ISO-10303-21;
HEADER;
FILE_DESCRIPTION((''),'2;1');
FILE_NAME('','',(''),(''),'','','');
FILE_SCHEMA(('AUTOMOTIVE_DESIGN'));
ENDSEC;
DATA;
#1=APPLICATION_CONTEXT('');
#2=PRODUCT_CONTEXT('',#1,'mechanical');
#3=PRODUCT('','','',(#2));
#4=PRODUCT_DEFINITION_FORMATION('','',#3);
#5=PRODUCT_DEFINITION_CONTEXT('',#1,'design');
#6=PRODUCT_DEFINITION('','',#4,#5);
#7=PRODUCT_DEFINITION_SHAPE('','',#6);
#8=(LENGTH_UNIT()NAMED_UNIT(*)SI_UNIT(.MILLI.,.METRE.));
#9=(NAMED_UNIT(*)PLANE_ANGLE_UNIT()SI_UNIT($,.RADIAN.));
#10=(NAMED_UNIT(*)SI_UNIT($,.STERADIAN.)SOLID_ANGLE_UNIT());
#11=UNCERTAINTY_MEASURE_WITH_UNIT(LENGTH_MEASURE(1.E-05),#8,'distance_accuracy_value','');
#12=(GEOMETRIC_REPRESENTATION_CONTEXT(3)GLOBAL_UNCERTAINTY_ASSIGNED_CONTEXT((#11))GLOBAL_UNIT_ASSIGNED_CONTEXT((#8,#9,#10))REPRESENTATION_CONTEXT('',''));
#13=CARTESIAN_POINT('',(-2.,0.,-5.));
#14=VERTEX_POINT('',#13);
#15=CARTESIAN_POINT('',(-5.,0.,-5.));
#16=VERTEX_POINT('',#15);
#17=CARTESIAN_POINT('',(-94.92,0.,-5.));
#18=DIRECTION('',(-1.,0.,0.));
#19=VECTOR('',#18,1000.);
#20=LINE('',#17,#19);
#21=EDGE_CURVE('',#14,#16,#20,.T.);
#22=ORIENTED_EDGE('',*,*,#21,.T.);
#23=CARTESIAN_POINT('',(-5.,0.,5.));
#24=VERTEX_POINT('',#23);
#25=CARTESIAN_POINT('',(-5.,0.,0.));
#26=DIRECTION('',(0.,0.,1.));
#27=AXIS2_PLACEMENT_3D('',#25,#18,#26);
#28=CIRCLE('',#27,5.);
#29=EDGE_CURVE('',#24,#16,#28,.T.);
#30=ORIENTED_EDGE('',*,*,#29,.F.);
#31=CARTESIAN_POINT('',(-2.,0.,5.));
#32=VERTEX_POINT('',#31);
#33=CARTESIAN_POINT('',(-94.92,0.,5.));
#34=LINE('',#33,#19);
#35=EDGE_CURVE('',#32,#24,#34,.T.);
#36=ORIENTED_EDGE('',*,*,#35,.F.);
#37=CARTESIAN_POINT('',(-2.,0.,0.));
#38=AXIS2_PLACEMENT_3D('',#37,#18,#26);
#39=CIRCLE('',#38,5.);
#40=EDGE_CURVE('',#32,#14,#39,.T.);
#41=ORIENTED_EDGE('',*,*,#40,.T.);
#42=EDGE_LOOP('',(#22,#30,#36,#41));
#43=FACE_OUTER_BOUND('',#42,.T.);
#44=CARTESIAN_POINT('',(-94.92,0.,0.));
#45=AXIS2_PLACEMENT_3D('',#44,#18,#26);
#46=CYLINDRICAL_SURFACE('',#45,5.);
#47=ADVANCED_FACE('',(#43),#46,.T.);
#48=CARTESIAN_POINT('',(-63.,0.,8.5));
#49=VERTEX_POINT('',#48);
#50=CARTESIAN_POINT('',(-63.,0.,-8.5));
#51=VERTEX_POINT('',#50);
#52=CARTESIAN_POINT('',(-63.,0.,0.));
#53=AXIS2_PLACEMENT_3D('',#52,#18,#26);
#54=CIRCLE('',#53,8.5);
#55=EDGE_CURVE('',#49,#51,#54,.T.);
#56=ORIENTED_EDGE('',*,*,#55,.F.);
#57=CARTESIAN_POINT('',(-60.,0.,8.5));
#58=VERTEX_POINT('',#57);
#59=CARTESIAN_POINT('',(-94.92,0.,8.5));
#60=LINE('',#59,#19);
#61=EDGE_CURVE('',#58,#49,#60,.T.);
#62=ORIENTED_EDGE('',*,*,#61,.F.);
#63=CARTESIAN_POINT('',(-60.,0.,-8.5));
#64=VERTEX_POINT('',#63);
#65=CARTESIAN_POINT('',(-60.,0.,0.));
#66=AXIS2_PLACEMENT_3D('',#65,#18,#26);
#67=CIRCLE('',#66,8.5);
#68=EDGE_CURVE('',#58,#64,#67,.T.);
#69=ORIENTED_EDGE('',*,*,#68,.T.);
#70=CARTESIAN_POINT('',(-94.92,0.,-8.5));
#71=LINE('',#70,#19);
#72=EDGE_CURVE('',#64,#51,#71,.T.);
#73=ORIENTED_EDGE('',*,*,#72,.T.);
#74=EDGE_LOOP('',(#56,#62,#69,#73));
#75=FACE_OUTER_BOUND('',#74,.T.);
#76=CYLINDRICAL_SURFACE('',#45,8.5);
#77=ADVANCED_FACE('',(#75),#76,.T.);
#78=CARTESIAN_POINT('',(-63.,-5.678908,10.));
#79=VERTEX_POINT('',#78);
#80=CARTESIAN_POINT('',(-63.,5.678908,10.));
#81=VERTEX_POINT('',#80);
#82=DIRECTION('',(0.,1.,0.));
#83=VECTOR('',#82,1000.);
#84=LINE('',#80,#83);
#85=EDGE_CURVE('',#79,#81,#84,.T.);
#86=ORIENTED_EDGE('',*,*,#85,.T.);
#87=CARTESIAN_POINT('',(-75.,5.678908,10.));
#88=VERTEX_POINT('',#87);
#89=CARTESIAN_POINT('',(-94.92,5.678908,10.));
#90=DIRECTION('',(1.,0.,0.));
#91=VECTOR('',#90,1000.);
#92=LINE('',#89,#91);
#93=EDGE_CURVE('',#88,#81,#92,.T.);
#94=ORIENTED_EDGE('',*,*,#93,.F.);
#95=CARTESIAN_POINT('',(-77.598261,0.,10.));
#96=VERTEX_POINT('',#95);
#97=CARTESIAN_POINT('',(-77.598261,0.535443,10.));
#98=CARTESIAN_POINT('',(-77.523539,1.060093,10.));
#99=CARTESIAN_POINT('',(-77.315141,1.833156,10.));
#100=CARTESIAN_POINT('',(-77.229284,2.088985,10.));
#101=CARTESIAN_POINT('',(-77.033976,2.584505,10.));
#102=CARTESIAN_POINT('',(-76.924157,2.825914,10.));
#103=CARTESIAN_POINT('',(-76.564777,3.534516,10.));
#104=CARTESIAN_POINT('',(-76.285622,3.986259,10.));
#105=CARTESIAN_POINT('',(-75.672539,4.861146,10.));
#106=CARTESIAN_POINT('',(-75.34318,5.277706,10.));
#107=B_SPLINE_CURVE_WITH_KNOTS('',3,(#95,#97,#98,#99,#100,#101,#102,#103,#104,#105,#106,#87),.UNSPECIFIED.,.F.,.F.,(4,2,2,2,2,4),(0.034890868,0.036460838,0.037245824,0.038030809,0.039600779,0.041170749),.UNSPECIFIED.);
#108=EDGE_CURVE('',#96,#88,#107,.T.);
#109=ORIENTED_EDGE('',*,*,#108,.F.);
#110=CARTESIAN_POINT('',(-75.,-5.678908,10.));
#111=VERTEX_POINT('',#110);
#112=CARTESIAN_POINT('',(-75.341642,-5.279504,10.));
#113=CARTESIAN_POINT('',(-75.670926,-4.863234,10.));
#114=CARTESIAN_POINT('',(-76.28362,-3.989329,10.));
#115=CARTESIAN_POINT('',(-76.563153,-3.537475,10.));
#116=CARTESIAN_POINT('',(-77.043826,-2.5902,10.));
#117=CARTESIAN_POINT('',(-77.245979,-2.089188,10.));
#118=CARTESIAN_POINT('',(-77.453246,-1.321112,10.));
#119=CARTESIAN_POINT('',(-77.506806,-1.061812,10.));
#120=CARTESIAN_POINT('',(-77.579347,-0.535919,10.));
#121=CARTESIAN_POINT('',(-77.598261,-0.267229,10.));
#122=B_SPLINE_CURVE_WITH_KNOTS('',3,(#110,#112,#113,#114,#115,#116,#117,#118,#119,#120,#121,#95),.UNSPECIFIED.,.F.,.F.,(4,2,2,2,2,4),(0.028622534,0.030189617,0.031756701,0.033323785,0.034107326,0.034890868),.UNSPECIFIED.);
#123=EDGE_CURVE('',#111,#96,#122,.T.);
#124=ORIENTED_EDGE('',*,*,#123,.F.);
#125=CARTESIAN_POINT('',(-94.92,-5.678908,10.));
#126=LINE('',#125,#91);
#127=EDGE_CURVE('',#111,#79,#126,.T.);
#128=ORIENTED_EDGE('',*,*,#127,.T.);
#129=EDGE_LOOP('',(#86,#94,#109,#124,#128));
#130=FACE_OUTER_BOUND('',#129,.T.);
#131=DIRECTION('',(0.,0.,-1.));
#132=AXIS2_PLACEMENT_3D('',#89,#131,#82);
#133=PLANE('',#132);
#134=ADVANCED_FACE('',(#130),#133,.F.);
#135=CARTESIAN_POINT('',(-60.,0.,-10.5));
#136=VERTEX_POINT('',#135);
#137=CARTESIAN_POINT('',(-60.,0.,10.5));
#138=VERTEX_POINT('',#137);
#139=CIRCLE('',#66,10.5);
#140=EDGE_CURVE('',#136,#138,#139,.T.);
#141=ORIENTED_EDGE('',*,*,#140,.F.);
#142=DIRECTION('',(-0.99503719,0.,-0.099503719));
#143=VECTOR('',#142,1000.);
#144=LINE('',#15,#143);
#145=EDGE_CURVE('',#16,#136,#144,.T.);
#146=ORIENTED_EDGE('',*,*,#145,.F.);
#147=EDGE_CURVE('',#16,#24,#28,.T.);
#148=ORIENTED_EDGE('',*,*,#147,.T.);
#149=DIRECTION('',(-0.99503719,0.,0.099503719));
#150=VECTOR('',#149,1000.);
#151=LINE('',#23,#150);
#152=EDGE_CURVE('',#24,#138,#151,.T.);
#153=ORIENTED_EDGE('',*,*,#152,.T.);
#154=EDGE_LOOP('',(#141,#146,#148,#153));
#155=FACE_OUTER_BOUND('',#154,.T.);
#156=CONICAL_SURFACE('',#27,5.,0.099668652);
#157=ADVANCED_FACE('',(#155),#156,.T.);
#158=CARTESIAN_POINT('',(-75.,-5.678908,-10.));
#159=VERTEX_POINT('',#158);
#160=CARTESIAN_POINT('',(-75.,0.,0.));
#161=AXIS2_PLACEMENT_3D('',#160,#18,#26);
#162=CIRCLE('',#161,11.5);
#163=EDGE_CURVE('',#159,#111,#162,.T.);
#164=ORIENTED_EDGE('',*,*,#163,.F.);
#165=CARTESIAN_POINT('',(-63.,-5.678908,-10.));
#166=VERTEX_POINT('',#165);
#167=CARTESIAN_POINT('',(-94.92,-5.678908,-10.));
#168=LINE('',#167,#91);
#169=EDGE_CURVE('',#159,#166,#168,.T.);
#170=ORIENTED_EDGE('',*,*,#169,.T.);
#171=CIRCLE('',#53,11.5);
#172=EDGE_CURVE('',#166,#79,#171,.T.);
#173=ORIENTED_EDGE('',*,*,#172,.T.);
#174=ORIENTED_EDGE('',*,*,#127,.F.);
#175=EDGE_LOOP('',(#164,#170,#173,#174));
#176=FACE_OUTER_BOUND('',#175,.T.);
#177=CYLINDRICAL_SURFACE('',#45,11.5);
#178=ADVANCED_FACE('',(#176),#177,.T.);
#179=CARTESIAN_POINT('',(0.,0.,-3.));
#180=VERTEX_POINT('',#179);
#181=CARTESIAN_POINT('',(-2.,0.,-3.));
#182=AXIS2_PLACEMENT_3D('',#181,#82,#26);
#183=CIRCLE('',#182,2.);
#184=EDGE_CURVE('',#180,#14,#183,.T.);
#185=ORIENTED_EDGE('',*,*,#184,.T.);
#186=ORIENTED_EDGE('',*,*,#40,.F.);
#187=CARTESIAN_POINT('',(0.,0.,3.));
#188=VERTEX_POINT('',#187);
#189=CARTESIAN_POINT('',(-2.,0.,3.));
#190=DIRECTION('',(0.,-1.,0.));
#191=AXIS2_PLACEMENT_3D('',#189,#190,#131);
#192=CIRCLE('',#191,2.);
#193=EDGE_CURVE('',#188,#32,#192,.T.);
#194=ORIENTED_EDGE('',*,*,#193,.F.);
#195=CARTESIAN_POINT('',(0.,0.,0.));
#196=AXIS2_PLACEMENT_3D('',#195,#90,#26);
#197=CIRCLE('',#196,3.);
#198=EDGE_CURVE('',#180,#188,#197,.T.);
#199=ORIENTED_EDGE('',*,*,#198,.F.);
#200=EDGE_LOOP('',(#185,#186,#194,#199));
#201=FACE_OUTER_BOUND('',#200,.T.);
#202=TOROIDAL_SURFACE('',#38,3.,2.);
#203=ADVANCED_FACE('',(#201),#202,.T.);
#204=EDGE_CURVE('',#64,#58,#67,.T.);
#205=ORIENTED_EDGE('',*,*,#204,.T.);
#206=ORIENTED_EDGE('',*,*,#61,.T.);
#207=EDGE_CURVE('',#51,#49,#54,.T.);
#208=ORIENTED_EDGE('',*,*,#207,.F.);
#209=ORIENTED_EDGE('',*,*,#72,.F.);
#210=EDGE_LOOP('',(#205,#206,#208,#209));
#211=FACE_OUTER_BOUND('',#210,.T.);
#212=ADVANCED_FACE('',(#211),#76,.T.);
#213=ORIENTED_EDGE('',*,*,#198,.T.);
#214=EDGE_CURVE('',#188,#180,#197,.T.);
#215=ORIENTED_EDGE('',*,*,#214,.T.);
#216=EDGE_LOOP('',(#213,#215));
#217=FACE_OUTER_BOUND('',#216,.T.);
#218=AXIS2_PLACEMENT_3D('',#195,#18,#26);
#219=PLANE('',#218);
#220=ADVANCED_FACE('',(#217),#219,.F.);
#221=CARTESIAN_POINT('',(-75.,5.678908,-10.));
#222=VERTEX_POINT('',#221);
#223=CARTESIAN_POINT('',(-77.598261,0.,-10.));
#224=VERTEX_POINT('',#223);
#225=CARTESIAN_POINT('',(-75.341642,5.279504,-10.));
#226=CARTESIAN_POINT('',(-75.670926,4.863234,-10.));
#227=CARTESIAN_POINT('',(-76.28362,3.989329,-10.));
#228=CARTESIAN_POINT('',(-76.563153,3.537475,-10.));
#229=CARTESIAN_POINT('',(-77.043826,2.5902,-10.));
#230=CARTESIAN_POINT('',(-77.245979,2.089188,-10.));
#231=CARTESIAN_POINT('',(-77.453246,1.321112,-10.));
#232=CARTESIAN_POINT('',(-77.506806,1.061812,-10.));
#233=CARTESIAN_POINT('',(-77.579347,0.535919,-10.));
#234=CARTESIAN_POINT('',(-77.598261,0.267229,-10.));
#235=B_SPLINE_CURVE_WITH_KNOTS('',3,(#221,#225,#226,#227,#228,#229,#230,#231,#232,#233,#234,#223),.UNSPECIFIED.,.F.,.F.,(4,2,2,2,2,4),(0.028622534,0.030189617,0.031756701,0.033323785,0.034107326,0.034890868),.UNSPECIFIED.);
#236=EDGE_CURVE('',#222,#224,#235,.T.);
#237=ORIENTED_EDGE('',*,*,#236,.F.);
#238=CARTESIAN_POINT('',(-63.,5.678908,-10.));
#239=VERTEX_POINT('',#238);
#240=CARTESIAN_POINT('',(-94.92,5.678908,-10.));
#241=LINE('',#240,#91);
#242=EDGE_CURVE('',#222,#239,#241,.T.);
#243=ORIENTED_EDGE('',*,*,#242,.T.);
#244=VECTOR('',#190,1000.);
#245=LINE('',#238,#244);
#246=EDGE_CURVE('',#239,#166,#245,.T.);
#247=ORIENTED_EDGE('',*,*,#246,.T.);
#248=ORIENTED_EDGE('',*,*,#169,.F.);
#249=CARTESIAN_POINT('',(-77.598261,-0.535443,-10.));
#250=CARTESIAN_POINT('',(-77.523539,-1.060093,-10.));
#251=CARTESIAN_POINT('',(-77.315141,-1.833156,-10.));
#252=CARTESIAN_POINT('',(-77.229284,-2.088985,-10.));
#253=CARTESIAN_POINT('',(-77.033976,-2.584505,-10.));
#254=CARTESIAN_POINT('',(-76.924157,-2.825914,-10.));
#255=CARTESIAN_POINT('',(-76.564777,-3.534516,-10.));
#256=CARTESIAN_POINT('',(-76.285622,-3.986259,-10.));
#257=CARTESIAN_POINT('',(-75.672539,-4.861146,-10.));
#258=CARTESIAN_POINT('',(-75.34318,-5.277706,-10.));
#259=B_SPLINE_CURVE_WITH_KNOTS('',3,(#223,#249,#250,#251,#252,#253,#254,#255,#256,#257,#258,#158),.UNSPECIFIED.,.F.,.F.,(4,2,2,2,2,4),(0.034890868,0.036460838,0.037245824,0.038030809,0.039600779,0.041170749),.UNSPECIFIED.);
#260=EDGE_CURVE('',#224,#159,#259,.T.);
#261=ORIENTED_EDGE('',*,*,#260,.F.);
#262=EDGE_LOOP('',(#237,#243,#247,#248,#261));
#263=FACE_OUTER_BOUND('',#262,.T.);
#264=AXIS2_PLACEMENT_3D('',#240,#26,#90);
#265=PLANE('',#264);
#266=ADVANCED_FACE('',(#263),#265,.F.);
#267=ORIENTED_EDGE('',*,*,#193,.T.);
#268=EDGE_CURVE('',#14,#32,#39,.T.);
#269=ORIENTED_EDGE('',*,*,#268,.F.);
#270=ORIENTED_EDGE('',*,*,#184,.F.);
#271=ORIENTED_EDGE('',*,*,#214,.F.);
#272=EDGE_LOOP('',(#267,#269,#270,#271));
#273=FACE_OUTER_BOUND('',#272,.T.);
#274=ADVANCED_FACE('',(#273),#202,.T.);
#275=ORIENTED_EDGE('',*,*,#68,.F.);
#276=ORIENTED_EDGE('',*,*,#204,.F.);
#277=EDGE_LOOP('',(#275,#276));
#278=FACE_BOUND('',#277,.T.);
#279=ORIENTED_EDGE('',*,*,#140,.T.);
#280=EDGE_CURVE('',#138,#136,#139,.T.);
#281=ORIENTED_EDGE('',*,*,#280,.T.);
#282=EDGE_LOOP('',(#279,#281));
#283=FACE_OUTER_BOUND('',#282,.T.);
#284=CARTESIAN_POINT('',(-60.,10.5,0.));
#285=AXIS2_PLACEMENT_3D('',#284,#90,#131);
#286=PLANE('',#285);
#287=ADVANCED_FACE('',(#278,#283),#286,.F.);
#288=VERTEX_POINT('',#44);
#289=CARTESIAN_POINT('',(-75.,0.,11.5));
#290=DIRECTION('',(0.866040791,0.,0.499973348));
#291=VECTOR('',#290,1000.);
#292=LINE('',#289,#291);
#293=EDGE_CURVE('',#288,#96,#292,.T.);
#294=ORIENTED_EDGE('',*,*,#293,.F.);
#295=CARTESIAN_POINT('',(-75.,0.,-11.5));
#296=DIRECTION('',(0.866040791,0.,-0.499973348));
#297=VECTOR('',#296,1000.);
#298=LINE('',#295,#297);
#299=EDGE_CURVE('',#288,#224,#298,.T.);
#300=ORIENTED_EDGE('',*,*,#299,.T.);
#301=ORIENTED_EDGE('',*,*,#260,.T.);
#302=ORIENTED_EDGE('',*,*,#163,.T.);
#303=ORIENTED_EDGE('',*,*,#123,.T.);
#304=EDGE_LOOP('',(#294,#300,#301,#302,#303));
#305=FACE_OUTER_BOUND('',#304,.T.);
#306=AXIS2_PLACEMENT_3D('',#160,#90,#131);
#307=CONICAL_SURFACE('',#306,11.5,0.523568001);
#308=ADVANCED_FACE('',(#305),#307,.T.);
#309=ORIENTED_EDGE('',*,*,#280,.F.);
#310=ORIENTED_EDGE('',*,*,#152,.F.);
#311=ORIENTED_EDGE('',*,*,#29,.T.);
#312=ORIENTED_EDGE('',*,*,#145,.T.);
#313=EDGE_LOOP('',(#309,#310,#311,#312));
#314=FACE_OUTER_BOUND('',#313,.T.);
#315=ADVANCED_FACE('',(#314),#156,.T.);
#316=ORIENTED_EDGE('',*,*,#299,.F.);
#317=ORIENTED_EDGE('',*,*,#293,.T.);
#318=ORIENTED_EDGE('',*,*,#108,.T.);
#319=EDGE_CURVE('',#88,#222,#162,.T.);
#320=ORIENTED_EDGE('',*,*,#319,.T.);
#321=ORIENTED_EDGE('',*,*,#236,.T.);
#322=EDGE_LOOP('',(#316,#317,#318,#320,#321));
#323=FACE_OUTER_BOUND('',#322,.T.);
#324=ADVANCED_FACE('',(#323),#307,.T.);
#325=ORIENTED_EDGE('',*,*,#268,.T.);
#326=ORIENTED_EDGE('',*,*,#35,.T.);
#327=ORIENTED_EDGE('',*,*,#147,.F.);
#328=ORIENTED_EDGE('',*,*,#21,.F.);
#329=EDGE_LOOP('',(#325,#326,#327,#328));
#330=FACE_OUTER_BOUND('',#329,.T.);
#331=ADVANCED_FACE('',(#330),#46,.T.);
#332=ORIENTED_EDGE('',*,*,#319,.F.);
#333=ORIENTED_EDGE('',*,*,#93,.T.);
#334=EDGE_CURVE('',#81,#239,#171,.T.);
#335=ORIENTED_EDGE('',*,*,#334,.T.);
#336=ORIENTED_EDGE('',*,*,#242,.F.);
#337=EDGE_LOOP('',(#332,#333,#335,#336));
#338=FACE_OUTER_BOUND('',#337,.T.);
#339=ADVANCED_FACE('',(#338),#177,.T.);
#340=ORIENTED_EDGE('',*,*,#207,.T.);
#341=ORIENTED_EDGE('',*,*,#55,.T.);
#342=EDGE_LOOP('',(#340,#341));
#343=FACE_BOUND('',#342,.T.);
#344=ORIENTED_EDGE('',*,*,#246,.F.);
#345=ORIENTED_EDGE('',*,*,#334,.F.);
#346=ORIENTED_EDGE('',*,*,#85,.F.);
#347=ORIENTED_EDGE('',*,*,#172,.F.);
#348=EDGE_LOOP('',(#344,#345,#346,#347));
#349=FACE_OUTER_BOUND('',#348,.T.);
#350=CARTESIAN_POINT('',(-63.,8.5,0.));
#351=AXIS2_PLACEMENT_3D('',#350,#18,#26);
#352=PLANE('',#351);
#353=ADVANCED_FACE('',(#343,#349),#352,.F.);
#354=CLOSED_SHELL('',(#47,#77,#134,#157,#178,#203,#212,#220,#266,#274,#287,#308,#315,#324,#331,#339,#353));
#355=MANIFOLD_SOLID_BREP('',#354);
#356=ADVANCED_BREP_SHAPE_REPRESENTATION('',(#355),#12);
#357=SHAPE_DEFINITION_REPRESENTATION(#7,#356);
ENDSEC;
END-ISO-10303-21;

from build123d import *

# Parameters (mm, degrees)
FILLET1_R          = 2
CUT_EXTRUDE1_DEPTH = 66.065351763


with BuildPart() as part:
    # Sketch1 → Revolve1 (revolve)
    with BuildSketch(Plane.XY, mode=Mode.PRIVATE) as revolve1_sk:
        Polygon((0, 0), (0, 5), (-5, 5), (-60, 10.5), (-60, 8.5), (-63, 8.5), (-63, 11.5), (-75, 11.5), (-94.92, 0), align=None)
    revolve(revolve1_sk.sketch.rotate(Axis((-94.92, 0, 0), (1, 0, 0)), 90), axis=Axis((-94.92, 0, 0), (1, 0, 0)))

    # Fillet1
    fillet1_edges = [part.edges().sort_by_distance(p)[0] for p in [
        (0, 0, -5),
    ]]
    fillet(fillet1_edges, radius=FILLET1_R)

    # Sketch2 → Cut-Extrude1 (cut, through all)
    with BuildSketch(Plane(origin=(-63, 0, 0), x_dir=(0, 0, -1), z_dir=(1, 0, 0))):
        with BuildLine():
            Line((-10, 5.678908346), (-10, -5.678908346))
            ThreePointArc((-10, -5.678908346), (-11.5, 0), (-10, 5.678908346))
        make_face()
        with BuildLine():
            Line((10, 5.678908346), (10, -5.678908346))
            ThreePointArc((10, -5.678908346), (11.5, 0), (10, 5.678908346))
        make_face()
    extrude(amount=-CUT_EXTRUDE1_DEPTH, mode=Mode.SUBTRACT)


solid = part.part
